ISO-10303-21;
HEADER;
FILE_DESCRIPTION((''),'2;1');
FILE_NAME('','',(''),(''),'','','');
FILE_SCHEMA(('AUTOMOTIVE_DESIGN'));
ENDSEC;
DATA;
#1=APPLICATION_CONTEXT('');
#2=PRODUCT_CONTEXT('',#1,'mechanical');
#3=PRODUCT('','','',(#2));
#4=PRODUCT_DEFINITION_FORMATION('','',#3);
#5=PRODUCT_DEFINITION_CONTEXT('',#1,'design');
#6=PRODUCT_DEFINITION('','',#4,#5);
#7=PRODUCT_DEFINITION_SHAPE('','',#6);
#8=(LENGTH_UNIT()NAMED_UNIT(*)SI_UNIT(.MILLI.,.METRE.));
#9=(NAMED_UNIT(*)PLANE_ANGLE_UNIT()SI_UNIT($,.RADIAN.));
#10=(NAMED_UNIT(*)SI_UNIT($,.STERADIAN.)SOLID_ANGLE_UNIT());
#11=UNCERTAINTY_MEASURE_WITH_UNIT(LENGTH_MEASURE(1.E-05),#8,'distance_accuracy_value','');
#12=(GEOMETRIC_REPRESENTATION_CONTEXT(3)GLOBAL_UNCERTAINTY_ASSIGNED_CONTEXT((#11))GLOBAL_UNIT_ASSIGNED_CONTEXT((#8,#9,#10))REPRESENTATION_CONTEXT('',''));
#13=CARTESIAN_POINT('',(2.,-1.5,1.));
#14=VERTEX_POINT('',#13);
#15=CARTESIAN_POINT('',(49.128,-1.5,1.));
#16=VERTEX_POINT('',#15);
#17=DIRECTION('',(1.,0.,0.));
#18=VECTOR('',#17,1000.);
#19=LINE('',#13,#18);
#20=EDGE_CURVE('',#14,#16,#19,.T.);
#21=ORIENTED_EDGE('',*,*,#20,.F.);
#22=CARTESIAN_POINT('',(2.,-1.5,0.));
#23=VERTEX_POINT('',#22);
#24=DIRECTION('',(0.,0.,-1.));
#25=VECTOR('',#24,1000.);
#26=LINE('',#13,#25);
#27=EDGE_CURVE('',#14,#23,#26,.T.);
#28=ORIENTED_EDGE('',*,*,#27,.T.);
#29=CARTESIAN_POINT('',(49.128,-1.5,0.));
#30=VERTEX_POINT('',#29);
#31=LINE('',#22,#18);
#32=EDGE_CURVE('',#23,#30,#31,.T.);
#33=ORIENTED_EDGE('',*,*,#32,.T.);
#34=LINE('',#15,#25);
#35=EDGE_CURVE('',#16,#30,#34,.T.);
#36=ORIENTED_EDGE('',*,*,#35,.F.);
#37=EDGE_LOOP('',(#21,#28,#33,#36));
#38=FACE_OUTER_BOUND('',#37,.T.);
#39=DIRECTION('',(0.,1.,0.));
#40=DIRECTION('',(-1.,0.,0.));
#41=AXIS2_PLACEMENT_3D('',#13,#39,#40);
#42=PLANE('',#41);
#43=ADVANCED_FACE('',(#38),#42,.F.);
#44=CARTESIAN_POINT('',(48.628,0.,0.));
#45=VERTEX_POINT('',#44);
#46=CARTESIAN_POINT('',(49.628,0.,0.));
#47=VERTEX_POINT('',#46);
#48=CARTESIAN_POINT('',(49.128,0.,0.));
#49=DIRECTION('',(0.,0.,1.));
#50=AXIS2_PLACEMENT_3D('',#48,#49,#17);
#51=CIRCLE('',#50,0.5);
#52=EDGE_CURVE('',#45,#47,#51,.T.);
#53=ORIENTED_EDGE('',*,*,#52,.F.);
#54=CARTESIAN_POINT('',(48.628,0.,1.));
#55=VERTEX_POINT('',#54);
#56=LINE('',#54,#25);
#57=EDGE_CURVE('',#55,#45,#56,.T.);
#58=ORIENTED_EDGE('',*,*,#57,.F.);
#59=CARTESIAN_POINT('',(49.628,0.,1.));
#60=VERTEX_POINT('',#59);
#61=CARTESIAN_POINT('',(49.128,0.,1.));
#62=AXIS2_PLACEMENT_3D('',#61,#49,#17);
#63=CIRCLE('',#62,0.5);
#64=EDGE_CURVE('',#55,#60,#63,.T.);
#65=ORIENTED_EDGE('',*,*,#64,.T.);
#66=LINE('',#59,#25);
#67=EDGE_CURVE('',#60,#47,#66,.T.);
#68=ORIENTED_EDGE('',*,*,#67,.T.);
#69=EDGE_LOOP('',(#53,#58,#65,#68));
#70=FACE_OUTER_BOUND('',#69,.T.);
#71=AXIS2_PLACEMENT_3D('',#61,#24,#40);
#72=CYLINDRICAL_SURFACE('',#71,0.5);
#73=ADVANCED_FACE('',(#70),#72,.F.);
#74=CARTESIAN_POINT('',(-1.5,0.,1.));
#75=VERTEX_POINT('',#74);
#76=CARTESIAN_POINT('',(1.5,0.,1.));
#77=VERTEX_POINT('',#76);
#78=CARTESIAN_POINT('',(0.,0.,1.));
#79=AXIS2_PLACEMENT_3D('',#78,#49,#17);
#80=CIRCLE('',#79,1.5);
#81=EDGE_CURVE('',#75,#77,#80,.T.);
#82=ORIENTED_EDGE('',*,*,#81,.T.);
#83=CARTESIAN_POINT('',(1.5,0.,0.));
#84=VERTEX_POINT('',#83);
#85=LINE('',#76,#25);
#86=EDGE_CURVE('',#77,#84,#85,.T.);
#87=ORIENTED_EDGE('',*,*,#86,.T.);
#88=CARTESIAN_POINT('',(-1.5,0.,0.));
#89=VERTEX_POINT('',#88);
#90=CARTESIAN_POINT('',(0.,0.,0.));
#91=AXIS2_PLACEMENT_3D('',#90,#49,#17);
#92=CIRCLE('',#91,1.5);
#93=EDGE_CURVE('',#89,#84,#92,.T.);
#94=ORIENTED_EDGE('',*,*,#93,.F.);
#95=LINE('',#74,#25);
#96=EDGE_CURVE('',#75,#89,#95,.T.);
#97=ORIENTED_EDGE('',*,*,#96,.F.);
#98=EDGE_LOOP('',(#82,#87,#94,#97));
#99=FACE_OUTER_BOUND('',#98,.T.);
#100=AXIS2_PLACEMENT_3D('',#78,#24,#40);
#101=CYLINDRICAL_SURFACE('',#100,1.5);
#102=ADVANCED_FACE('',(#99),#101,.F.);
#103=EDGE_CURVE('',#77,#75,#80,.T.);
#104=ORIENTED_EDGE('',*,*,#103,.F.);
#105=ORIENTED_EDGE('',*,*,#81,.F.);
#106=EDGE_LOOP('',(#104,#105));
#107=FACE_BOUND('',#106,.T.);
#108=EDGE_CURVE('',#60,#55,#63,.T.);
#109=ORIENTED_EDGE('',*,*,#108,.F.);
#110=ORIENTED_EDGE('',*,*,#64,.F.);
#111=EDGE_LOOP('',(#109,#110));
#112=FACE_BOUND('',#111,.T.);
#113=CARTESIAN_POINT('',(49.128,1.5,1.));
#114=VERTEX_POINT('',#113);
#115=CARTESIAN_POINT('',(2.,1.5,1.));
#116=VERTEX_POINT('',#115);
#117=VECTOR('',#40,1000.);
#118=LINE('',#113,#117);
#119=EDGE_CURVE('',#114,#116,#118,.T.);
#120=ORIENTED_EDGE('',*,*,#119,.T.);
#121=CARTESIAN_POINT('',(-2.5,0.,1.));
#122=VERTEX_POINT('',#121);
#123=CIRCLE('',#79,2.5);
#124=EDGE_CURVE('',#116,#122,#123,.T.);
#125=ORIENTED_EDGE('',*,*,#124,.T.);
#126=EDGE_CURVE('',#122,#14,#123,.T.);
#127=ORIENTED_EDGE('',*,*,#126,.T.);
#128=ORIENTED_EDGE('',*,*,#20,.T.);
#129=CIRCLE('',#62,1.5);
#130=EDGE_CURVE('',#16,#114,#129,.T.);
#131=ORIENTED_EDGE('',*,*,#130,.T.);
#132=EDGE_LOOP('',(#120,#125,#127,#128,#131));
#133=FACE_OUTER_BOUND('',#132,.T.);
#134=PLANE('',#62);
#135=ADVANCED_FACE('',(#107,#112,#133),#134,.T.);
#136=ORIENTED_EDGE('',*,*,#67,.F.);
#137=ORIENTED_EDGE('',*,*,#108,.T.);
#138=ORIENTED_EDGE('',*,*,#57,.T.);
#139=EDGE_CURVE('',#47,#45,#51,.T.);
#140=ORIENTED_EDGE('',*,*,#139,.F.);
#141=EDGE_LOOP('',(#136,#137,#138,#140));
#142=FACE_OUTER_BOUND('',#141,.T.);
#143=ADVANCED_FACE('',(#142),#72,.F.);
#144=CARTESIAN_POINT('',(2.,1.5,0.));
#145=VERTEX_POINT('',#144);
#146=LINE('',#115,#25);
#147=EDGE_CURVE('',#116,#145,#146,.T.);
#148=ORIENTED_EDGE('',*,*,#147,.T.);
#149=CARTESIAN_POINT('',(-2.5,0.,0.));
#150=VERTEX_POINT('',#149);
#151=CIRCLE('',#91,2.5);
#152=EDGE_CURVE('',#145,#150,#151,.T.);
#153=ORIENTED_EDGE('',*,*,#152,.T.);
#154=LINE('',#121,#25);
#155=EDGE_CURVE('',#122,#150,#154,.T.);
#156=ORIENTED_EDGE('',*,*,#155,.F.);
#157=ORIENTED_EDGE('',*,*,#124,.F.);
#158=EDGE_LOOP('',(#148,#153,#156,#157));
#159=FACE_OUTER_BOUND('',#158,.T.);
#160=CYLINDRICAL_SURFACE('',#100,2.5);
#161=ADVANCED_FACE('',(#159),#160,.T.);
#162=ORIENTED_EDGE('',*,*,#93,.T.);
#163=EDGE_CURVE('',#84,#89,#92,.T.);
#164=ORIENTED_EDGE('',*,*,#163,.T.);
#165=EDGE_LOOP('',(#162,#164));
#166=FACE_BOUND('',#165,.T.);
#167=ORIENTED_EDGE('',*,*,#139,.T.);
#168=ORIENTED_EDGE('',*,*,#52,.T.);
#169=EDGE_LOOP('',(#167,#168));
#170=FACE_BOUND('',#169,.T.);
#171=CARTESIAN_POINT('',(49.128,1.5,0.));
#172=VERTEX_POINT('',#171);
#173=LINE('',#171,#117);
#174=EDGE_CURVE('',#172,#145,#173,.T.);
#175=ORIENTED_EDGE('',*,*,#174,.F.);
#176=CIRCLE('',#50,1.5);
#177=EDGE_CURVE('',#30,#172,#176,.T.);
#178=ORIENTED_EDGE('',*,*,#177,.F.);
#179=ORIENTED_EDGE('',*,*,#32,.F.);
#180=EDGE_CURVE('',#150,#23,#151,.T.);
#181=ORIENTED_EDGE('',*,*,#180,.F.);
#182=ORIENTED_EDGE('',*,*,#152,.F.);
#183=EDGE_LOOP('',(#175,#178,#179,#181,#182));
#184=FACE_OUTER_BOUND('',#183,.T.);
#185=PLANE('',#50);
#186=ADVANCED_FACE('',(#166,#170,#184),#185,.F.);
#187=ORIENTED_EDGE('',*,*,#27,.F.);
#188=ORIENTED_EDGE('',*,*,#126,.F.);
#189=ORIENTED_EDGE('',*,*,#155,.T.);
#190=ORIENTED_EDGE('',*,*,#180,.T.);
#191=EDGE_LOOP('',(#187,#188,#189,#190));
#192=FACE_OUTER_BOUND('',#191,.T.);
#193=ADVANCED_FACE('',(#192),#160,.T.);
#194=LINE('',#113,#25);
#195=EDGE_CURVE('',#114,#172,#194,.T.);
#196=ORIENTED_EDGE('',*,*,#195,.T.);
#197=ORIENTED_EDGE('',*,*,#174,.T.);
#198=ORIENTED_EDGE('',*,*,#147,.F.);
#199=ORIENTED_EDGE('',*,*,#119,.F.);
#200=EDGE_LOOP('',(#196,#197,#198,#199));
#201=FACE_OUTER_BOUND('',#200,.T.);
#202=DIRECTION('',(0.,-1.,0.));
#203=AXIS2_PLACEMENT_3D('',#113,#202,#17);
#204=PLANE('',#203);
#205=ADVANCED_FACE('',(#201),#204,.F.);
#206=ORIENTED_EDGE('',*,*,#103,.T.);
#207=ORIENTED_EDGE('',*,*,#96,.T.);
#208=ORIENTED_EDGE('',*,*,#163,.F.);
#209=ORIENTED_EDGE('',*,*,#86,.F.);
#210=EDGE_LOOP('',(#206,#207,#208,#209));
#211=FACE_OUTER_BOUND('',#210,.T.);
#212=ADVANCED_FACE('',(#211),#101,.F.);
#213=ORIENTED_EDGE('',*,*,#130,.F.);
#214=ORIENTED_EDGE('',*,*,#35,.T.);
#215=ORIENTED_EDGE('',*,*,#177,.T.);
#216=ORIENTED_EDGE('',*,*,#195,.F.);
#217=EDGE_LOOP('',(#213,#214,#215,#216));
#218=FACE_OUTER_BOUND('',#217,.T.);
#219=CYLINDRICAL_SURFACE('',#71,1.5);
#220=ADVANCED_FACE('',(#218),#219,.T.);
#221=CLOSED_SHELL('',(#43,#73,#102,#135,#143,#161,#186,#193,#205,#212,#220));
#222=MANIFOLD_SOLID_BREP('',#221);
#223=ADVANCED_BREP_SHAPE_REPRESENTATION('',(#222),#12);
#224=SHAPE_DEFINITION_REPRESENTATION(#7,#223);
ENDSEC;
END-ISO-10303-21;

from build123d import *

# Parameters (mm, degrees)
SKETCH_2_R           = 1.5
SKETCH_2_R_2         = 0.5
BOSS_EXTRUDE_1_DEPTH = 1


with BuildPart() as part:
    # Sketch 2 → Boss-Extrude 1 (new body)
    with BuildSketch(Plane.XY):
        with BuildLine():
            Line((49.128, 1.5), (2, 1.5))
            ThreePointArc((2, 1.5), (-2.5, 0), (2, -1.5))
            Line((2, -1.5), (49.128, -1.5))
            ThreePointArc((49.128, -1.5), (50.628, 0), (49.128, 1.5))
        make_face()
        Circle(SKETCH_2_R, mode=Mode.SUBTRACT)
        with Locations((49.128, 0)):
            Circle(SKETCH_2_R_2, mode=Mode.SUBTRACT)
    extrude(amount=BOSS_EXTRUDE_1_DEPTH)


solid = part.part
